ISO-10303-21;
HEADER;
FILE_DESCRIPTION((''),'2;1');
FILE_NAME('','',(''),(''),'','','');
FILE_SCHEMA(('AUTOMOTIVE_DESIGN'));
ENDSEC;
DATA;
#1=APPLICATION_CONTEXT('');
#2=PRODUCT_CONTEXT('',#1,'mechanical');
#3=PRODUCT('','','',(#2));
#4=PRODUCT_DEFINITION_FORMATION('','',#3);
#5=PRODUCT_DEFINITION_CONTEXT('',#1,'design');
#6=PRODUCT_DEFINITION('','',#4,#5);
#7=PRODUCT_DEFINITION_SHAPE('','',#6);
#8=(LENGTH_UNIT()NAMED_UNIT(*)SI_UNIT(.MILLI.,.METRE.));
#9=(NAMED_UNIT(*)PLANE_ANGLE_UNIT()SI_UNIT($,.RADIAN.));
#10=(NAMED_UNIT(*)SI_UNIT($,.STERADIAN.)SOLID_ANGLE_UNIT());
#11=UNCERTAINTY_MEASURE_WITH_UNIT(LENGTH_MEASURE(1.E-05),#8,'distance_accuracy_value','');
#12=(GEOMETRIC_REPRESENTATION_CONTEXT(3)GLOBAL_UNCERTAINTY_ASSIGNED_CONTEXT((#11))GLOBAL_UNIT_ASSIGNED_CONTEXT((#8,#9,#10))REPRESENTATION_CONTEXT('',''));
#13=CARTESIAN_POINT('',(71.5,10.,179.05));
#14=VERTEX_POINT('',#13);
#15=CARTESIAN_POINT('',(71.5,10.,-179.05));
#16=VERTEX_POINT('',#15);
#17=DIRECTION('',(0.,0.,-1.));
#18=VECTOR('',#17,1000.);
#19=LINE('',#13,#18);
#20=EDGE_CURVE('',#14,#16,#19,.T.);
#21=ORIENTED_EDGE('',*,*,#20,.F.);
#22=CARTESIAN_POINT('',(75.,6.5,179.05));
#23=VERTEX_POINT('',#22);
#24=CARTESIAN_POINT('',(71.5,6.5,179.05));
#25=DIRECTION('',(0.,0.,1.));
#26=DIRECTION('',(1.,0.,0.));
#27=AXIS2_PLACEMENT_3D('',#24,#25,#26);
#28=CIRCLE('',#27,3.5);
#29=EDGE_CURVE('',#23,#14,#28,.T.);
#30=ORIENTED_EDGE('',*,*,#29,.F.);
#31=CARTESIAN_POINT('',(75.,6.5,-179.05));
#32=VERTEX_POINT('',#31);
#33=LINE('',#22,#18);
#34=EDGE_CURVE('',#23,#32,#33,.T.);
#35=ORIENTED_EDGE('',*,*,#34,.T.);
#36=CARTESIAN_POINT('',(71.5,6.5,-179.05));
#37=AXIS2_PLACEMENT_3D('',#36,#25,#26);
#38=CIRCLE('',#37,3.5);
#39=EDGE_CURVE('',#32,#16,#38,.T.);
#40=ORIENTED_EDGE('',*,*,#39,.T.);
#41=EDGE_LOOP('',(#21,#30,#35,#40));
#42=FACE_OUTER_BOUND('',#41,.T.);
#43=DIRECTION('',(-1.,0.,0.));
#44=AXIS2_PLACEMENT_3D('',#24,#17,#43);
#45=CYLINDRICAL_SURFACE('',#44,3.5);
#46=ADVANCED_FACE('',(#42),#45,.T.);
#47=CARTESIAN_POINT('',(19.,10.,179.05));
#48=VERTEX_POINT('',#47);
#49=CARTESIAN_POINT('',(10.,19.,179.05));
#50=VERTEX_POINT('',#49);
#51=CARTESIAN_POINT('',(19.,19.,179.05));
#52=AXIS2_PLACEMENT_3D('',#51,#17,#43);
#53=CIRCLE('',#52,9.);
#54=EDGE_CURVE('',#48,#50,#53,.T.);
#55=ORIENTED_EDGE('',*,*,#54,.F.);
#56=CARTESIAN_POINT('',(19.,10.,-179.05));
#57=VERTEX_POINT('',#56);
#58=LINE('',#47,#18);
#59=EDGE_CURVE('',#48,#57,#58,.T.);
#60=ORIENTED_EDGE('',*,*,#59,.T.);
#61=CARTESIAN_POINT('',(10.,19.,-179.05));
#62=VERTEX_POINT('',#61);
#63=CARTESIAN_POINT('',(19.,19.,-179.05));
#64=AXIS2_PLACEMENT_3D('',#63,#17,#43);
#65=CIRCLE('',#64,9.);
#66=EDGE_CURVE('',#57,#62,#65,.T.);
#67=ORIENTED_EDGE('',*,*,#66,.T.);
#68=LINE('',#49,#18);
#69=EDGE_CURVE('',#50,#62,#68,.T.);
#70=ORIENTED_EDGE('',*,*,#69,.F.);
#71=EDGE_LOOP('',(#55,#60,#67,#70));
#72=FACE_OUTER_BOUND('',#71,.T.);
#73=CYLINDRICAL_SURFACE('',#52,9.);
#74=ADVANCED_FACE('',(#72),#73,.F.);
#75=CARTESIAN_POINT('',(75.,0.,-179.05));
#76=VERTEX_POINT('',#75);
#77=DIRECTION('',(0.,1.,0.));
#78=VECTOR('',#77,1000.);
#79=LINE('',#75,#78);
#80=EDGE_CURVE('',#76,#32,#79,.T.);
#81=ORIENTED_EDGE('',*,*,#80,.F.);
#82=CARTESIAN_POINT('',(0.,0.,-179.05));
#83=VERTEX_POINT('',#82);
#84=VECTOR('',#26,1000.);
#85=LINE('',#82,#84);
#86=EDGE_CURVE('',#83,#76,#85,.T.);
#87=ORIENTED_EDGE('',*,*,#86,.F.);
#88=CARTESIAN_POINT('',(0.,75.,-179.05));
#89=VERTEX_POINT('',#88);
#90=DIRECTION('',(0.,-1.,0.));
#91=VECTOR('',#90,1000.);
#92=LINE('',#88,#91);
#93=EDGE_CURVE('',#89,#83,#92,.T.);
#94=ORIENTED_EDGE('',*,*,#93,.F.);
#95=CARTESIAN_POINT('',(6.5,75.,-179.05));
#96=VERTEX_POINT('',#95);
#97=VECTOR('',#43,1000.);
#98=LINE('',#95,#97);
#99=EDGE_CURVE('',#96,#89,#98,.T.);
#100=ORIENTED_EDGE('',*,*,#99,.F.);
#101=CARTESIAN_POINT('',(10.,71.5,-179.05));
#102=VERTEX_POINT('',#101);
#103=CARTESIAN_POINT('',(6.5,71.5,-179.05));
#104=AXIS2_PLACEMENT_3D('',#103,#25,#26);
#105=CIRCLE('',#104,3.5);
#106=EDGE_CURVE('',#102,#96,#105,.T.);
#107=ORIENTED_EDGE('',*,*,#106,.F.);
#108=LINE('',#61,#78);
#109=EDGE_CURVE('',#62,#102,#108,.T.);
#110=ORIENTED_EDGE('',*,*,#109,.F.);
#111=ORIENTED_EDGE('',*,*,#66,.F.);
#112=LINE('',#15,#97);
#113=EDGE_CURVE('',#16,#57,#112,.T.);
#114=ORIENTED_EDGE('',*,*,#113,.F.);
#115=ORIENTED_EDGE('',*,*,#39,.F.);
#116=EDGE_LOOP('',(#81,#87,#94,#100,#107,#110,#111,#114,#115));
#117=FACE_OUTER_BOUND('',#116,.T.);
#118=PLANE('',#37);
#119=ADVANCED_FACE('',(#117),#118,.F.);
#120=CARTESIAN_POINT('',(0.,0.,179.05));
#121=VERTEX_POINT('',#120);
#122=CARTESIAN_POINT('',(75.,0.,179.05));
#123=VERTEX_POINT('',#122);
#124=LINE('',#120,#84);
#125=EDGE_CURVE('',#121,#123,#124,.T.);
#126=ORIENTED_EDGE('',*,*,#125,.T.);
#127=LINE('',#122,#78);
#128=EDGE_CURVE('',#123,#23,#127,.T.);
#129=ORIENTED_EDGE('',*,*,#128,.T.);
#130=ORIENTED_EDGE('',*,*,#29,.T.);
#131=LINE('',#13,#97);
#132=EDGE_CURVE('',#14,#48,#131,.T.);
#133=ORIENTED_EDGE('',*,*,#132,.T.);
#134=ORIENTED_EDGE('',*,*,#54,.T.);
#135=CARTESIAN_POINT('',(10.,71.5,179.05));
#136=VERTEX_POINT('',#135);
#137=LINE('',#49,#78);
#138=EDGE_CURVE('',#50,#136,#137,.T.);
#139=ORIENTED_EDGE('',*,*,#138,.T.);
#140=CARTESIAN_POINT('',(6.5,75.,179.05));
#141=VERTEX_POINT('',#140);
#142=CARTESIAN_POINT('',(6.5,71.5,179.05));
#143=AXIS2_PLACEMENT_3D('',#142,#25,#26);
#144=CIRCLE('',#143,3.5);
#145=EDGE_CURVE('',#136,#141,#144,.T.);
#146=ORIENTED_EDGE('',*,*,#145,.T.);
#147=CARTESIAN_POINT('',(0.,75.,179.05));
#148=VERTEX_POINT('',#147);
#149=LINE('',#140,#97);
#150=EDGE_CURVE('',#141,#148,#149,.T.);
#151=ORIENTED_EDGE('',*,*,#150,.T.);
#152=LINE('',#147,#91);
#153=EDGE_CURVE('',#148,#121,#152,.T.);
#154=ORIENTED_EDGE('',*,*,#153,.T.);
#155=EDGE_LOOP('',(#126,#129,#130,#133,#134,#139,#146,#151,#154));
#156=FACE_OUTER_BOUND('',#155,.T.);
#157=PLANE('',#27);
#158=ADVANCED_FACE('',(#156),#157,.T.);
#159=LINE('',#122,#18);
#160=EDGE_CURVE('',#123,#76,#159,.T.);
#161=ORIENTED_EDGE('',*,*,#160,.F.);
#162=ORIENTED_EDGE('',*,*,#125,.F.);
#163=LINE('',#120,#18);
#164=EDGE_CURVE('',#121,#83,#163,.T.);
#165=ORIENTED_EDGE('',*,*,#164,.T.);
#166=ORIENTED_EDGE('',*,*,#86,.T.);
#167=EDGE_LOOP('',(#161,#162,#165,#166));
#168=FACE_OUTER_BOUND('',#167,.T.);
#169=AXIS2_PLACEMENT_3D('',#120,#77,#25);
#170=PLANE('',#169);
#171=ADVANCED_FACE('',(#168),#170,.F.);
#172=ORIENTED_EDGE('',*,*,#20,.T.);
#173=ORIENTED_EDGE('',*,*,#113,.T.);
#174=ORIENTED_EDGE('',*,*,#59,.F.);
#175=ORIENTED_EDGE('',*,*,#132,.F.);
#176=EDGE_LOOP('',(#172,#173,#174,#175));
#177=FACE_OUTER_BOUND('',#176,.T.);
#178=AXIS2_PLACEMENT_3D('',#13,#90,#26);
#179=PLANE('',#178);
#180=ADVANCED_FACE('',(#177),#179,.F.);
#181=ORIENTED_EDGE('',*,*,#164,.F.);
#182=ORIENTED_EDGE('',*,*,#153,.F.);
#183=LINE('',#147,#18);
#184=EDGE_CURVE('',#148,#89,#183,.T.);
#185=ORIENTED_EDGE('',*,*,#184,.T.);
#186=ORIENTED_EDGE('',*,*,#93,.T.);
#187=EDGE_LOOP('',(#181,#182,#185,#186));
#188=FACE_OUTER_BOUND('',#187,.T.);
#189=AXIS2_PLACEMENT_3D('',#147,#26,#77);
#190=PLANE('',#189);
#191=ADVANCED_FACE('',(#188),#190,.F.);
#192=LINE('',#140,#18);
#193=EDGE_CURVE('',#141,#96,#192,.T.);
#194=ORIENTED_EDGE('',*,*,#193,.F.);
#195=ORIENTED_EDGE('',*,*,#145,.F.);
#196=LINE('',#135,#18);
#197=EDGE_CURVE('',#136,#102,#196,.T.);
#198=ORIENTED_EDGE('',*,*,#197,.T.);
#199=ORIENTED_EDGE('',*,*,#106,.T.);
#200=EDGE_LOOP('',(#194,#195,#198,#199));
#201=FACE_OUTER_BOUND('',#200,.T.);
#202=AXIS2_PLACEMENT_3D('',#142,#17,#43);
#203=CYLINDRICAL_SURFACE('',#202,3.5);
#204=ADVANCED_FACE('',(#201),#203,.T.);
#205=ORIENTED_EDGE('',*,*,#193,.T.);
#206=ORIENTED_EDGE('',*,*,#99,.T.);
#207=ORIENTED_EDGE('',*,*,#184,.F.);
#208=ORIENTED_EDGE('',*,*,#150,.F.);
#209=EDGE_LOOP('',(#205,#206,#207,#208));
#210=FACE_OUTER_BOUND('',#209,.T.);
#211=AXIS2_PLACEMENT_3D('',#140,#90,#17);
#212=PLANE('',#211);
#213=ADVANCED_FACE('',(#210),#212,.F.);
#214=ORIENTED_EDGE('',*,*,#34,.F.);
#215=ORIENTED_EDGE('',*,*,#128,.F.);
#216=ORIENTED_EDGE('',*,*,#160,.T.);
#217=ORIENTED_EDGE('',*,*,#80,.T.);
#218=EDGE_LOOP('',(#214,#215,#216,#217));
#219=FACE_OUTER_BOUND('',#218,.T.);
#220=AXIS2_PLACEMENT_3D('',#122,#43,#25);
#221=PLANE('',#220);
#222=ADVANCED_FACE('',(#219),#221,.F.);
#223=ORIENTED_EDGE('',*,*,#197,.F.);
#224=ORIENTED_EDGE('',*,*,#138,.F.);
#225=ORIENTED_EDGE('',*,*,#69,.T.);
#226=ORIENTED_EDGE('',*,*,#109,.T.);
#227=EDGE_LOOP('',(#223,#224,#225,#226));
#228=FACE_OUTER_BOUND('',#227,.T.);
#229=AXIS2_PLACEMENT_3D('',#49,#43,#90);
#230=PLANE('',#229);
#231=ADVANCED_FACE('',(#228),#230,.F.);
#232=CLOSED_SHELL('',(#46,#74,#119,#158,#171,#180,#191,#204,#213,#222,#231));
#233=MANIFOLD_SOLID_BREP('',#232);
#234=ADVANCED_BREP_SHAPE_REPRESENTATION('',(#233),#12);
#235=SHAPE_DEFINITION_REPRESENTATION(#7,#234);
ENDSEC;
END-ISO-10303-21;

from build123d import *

# Parameters (mm, degrees)
BOSS_EXTRUDE1_DEPTH = 179.05


with BuildPart() as part:
    # Sketch1 → Boss-Extrude1 (new, symmetric)
    with BuildSketch(Plane.XY):
        with BuildLine():
            Line((0, 75), (0, 0))
            Line((0, 0), (75, 0))
            Line((75, 0), (75, 6.5))
            ThreePointArc((75, 6.5), (73.974873734, 8.974873734), (71.5, 10))
            Line((71.5, 10), (19, 10))
            ThreePointArc((19, 10), (12.636038969, 12.636038969), (10, 19))
            Line((10, 19), (10, 71.5))
            ThreePointArc((10, 71.5), (8.974873734, 73.974873734), (6.5, 75))
            Line((6.5, 75), (0, 75))
        make_face()
    extrude(amount=BOSS_EXTRUDE1_DEPTH, both=True)


solid = part.part
